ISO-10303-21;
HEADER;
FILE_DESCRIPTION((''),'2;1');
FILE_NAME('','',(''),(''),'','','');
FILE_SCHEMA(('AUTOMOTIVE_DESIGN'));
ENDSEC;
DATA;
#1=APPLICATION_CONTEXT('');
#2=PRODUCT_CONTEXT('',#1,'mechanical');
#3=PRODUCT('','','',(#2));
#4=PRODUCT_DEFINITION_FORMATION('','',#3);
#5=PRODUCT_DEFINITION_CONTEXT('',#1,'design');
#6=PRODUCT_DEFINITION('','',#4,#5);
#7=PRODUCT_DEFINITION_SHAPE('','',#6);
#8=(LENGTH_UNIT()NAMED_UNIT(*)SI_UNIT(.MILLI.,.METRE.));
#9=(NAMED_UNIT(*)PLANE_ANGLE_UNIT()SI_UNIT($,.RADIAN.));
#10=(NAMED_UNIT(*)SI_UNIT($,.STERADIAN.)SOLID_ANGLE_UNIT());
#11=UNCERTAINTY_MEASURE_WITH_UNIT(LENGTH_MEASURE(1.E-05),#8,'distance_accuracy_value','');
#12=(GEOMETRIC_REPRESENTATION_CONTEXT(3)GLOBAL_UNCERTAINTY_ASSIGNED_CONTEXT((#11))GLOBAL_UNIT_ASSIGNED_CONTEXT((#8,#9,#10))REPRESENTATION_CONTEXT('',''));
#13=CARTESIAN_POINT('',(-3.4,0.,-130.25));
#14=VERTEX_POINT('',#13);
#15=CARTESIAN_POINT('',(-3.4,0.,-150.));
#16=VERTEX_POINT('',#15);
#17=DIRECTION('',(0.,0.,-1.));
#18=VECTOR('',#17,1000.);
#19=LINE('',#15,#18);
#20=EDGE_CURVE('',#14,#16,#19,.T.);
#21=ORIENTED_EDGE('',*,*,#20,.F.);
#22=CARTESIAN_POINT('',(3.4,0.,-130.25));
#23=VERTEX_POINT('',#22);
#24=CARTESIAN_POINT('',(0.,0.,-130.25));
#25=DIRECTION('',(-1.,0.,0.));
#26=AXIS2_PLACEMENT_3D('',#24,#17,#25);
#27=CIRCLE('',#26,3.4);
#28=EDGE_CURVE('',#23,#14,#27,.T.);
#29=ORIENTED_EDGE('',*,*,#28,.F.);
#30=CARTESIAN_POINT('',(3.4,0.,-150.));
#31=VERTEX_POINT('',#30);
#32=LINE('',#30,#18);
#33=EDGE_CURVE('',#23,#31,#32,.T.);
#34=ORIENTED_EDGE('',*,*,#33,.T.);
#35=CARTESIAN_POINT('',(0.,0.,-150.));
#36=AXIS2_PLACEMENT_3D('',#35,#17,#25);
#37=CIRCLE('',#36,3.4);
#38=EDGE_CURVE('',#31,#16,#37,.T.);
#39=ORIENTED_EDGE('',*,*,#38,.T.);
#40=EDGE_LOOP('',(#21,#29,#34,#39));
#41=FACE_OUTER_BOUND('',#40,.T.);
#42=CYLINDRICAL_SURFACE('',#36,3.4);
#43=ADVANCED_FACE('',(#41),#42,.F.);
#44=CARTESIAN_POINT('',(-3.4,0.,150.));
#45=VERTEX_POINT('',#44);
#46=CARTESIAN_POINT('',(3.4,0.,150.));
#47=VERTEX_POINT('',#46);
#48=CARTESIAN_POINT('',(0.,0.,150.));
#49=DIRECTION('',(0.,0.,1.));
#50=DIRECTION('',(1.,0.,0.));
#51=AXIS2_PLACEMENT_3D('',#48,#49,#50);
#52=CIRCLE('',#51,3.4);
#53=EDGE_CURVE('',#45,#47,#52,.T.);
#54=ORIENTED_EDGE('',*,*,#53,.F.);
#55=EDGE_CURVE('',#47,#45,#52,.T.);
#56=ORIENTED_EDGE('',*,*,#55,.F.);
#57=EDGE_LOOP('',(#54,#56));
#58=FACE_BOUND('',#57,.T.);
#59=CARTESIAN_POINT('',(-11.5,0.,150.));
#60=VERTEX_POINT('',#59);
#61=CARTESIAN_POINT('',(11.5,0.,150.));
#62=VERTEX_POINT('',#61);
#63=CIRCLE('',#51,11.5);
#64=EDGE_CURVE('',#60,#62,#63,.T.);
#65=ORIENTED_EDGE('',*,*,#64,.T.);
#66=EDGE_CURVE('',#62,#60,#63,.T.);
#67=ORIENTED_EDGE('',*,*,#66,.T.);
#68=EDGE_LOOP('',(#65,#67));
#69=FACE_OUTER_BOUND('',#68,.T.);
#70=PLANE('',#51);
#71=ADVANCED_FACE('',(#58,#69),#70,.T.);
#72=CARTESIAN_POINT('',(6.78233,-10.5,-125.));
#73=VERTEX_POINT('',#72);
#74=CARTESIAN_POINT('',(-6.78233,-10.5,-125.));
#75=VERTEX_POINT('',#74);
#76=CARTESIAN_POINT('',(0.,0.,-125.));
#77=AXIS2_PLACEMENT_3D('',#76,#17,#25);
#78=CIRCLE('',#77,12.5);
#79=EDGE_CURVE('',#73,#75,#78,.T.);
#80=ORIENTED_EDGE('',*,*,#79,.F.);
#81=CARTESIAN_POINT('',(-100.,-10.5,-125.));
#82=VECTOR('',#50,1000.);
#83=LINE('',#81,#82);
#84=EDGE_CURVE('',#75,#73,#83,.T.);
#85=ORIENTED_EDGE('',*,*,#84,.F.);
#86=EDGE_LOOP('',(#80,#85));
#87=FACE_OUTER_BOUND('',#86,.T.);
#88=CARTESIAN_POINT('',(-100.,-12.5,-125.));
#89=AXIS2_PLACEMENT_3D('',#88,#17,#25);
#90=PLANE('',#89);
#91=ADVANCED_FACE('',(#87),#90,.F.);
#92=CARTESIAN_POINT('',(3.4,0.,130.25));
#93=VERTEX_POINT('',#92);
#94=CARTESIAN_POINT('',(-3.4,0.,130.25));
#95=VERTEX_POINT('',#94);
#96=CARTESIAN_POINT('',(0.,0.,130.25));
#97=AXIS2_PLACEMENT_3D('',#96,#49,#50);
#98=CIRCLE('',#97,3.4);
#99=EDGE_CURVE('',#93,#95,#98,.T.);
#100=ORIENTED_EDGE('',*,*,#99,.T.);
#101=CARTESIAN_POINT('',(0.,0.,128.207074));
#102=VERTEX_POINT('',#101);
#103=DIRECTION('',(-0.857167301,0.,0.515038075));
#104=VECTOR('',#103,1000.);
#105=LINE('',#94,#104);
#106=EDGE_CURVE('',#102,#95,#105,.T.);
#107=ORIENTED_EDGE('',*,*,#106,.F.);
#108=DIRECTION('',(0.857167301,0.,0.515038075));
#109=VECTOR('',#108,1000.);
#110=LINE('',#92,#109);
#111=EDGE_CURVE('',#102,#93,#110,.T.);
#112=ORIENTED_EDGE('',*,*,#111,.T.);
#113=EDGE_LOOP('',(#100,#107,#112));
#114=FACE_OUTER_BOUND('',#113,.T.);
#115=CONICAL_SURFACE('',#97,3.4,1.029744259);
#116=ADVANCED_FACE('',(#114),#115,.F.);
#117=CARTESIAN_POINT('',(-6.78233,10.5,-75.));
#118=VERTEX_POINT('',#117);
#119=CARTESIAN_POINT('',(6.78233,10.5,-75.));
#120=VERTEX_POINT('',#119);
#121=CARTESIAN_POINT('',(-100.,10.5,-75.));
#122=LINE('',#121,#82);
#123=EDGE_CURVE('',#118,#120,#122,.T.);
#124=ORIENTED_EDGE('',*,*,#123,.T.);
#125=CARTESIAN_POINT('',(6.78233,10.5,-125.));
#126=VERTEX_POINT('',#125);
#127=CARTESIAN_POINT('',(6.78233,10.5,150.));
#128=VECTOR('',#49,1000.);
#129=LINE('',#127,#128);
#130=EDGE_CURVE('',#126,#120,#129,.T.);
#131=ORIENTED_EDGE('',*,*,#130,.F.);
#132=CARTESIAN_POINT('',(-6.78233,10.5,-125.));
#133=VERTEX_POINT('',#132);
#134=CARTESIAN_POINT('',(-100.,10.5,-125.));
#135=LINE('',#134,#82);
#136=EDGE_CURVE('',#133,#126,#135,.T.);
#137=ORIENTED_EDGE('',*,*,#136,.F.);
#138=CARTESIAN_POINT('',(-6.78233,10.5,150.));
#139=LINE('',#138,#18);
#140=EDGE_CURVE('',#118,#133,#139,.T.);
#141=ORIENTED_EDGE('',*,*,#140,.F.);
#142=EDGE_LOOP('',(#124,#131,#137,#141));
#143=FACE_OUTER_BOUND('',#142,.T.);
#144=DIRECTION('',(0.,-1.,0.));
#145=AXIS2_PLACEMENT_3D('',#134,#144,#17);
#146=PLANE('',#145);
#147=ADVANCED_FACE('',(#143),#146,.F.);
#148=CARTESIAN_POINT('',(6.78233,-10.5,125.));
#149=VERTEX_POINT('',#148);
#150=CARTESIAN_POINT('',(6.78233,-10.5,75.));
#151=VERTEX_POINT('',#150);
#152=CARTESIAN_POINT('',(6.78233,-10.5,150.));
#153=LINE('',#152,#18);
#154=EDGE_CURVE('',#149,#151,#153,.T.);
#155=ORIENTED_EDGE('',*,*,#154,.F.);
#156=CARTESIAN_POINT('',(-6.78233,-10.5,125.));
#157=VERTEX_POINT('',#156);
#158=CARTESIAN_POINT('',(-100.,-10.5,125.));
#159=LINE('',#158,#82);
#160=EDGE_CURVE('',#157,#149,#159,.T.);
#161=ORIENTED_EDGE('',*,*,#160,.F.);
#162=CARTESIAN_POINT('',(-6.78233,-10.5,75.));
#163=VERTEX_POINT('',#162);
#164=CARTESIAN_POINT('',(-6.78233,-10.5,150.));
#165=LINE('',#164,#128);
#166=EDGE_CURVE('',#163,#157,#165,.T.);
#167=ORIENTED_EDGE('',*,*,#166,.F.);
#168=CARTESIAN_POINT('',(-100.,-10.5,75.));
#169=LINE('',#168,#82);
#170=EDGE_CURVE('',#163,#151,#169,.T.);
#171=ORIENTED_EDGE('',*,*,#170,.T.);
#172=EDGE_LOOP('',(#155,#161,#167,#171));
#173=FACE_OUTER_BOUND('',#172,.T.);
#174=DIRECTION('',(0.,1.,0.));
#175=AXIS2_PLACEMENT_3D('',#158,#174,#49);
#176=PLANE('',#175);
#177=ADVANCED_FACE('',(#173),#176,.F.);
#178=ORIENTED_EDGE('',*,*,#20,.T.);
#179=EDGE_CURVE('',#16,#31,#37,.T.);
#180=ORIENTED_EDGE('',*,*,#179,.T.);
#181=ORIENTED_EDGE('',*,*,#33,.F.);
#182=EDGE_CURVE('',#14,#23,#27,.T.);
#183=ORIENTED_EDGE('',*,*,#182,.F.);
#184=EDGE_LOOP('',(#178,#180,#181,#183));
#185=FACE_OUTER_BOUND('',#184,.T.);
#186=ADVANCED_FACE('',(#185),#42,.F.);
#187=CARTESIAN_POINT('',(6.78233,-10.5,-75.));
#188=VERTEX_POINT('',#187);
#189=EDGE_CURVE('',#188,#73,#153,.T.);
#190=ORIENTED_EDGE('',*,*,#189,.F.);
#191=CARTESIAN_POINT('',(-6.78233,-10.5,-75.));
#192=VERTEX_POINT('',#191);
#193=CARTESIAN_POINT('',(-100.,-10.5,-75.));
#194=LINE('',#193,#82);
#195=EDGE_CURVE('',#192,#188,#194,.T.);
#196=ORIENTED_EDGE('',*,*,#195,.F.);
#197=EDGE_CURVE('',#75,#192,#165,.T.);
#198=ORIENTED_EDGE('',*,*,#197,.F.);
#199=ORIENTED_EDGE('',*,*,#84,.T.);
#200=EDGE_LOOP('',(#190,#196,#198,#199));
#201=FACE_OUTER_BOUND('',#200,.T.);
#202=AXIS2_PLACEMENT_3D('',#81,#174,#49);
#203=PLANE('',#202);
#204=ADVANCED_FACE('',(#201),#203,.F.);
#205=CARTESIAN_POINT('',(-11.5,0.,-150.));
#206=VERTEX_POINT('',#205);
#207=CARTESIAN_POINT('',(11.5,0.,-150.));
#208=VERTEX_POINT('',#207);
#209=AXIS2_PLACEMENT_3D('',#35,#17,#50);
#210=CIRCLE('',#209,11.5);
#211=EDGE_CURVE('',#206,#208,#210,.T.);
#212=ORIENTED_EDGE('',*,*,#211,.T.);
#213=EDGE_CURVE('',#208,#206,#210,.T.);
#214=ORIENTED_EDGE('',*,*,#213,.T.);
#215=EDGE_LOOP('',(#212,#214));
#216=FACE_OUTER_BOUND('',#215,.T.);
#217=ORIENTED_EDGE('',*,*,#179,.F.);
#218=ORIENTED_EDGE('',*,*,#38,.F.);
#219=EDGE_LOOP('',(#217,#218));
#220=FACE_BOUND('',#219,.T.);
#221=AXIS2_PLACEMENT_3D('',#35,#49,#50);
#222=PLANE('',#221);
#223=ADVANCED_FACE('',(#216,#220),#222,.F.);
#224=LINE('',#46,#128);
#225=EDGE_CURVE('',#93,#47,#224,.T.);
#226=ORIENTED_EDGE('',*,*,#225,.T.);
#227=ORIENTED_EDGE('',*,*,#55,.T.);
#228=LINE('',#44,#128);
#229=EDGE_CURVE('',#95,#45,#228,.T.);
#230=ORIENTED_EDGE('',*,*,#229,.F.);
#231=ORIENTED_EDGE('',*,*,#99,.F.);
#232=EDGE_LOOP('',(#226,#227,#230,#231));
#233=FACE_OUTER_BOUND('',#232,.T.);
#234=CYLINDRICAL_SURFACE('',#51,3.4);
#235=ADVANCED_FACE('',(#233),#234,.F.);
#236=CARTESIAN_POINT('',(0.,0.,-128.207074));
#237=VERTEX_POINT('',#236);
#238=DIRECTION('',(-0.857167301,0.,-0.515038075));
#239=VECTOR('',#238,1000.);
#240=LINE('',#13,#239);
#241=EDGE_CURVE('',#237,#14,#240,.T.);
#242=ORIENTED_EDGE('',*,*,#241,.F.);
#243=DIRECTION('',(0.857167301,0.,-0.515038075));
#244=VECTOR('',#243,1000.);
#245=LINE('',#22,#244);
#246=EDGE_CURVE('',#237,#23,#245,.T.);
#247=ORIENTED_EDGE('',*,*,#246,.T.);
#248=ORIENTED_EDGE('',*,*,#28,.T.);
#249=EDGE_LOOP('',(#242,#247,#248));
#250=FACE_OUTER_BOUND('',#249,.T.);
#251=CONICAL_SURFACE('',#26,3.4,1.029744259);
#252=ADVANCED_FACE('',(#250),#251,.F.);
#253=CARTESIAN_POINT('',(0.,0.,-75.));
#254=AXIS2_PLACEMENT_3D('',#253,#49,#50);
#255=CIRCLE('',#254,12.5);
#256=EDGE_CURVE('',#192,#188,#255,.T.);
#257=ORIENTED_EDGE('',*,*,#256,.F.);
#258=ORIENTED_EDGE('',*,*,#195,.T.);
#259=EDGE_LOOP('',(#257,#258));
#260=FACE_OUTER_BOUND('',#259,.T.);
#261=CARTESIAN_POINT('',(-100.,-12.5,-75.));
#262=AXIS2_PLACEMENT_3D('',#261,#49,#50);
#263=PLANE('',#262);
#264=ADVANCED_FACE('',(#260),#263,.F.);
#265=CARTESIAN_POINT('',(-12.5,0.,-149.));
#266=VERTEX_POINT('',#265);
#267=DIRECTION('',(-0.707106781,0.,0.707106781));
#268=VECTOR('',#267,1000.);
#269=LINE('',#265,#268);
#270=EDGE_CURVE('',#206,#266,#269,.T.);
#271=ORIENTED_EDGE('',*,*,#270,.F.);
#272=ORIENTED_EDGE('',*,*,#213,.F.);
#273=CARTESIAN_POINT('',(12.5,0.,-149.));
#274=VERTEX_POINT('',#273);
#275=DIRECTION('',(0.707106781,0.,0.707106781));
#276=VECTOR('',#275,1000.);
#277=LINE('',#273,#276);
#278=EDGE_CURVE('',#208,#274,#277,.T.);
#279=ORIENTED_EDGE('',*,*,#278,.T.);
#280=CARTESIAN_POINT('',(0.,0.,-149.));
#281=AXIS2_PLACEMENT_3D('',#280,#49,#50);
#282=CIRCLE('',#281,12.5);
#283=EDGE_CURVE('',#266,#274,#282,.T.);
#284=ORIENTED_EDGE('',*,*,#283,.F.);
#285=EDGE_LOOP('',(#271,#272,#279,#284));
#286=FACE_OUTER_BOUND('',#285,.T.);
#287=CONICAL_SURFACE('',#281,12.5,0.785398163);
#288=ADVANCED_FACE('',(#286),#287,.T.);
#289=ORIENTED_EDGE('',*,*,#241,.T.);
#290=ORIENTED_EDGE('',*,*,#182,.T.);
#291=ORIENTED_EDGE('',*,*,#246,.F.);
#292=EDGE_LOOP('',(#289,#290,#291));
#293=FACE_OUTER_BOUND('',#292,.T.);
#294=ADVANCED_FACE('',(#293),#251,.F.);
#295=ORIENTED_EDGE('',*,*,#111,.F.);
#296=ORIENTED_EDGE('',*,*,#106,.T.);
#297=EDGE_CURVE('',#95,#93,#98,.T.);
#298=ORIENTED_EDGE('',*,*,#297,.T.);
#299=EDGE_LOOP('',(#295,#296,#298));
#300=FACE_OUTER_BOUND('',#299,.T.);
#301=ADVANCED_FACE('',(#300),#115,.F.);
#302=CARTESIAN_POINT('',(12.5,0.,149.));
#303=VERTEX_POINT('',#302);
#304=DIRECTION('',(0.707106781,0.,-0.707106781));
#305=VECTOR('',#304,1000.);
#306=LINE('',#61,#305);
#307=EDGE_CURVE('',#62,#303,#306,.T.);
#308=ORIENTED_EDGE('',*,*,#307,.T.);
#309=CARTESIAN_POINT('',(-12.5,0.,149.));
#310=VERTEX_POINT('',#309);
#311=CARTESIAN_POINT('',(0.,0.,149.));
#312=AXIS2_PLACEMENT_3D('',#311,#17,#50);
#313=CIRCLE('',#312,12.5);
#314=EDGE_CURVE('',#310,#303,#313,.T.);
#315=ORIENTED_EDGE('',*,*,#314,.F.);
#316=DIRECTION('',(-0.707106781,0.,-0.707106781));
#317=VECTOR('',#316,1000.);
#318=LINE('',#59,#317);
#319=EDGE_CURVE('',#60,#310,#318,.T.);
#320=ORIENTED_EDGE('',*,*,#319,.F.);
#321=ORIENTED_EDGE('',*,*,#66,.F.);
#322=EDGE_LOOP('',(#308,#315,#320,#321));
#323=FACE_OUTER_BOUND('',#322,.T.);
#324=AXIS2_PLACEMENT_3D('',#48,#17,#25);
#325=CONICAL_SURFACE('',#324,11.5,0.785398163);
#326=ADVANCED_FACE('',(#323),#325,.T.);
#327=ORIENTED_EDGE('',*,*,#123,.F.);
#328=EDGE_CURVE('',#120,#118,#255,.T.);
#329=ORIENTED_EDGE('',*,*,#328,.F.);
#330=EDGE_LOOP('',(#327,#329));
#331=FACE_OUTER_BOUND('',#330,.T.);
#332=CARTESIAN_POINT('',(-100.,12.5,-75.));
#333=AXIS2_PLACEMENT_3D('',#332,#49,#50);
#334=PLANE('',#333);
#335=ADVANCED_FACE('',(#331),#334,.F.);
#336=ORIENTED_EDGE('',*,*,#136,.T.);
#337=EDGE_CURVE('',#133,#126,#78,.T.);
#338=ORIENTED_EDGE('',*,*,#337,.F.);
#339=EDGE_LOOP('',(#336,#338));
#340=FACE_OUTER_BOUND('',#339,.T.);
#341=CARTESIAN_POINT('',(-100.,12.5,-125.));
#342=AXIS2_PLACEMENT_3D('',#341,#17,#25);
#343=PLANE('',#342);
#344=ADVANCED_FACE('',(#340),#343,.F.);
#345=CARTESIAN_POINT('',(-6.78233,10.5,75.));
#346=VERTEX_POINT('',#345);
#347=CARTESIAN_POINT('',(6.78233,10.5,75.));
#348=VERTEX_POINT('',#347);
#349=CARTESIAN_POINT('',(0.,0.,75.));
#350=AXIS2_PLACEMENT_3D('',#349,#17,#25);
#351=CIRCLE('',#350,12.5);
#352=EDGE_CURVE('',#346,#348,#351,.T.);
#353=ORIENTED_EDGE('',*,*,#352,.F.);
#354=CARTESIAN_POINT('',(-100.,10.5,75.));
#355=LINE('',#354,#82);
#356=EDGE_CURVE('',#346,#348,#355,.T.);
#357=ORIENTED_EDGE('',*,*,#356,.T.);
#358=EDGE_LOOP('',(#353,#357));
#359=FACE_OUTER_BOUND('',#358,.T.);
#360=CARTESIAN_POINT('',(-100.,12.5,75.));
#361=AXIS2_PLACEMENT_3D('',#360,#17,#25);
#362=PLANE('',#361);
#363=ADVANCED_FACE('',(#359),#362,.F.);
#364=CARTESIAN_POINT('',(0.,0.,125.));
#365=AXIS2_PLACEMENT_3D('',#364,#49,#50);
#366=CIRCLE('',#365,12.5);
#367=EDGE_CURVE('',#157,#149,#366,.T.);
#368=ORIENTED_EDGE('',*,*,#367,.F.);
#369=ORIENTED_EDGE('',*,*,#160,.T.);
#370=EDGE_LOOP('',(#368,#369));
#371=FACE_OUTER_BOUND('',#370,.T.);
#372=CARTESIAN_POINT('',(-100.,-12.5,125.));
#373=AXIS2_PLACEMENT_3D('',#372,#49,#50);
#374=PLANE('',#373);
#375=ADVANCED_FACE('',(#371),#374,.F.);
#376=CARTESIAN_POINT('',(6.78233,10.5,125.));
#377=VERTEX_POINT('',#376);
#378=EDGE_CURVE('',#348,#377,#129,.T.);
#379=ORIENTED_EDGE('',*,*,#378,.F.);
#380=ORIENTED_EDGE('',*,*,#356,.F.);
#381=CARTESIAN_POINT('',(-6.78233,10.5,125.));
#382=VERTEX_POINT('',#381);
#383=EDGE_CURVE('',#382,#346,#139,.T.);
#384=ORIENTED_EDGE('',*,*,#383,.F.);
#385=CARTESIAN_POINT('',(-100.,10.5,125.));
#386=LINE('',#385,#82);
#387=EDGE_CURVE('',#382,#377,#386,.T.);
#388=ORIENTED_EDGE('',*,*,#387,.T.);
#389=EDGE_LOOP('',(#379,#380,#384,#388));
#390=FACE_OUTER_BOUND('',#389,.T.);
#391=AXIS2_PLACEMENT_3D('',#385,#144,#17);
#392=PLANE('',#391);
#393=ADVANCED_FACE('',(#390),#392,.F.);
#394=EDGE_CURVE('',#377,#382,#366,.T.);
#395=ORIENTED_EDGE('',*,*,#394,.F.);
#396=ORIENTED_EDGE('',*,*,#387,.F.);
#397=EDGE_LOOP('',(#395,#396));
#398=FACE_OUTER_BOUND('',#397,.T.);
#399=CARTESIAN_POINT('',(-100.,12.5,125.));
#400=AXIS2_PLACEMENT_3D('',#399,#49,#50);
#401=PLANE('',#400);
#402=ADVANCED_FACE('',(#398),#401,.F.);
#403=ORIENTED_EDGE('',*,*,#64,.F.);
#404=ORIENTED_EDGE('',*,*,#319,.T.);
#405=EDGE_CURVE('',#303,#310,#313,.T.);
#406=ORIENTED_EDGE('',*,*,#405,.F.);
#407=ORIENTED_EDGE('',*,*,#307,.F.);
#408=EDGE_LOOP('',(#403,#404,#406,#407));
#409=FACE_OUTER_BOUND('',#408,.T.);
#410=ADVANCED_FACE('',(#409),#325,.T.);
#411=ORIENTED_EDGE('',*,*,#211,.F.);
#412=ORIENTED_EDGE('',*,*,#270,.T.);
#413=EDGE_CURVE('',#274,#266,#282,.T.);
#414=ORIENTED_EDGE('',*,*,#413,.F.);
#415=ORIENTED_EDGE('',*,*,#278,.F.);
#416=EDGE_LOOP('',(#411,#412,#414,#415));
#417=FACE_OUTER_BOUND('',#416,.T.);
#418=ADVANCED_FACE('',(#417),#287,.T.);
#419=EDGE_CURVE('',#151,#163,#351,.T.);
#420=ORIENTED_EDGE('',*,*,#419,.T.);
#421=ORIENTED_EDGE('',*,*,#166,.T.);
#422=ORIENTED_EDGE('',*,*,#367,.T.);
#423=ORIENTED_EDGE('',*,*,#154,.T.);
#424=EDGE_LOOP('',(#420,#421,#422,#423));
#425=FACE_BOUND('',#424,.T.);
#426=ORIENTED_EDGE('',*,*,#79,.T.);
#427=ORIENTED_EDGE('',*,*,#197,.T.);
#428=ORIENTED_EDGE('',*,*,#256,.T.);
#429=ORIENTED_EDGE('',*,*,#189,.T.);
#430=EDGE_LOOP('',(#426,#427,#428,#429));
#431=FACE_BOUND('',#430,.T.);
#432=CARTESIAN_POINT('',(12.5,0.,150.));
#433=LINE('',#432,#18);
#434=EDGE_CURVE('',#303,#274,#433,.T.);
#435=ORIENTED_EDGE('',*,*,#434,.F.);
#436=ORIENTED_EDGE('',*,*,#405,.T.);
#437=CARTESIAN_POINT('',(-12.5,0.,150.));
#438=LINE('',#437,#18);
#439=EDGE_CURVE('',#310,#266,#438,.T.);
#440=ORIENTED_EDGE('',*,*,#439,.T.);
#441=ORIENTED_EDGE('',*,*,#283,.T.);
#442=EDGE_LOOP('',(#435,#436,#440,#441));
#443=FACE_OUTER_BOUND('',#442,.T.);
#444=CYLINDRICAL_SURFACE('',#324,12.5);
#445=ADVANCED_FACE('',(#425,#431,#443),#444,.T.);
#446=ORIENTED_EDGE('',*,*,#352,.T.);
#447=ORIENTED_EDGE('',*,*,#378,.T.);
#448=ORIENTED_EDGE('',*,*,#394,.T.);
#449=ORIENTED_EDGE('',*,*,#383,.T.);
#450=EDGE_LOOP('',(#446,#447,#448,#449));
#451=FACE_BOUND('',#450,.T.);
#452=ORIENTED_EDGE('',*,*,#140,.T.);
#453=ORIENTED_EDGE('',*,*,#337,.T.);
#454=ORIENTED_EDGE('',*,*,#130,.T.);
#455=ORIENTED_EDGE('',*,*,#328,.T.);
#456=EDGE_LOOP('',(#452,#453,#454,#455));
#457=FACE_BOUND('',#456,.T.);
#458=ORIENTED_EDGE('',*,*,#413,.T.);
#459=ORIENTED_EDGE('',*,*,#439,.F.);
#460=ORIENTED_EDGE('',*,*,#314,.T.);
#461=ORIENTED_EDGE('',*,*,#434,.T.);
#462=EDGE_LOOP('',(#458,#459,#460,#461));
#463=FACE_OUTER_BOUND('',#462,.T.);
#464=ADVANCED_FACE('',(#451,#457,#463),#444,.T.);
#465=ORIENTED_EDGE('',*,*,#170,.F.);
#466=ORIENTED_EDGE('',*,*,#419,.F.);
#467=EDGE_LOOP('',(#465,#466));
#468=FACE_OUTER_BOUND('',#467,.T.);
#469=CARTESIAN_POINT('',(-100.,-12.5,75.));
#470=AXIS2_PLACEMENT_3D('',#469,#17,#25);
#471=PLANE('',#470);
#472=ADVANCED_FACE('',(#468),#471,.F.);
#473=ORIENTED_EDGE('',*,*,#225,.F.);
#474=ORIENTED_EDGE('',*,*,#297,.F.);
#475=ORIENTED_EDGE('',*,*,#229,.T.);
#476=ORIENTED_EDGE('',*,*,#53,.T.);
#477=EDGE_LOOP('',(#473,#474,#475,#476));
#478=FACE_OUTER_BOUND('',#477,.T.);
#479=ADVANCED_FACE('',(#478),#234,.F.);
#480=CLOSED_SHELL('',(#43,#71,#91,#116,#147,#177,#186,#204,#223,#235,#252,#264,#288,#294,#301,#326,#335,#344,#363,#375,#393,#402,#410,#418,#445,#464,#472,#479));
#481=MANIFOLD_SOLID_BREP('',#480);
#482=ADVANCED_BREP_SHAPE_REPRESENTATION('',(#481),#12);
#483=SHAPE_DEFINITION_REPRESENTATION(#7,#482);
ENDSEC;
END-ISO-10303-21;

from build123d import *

# Parameters (mm, degrees)
SKETCH_1_R          = 12.5
EXTRUDE_1_DEPTH     = 150
SKETCH_2_W          = 50
SKETCH_2_H          = 2
CUT_EXTRUDE_1_DEPTH = 100
CHAMFER_1_SIZE      = 1


with BuildPart() as part:
    # 草图1 → 凸台-拉伸1 (new, symmetric)
    with BuildSketch(Plane.XY):
        Circle(SKETCH_1_R)
    extrude(amount=EXTRUDE_1_DEPTH, both=True)

    # 草图2 → 切除-拉伸1 (cut, symmetric)
    with BuildSketch(Plane(origin=(0, 0, 0), x_dir=(0, 0, -1), z_dir=(1, 0, 0))):
        with Locations((-100, 11.5)):
            Rectangle(SKETCH_2_W, SKETCH_2_H)
        with Locations((-100, -11.5)):
            Rectangle(SKETCH_2_W, SKETCH_2_H)
        with Locations((100, -11.5)):
            Rectangle(SKETCH_2_W, SKETCH_2_H)
        with Locations((100, 11.5)):
            Rectangle(SKETCH_2_W, SKETCH_2_H)
    extrude(amount=CUT_EXTRUDE_1_DEPTH, both=True, mode=Mode.SUBTRACT)

    # 倒角1
    chamfer_1_edges = [part.edges().sort_by_distance(p)[0] for p in [
        (-12.5, 0, -150),
        (-12.5, 0, 150),
    ]]
    chamfer(chamfer_1_edges, length=CHAMFER_1_SIZE)

    # 草图4 → M8 螺纹孔1 (revolve, cut)
    with BuildSketch(Plane(origin=(0, 0, -150), x_dir=(0, 1, 0), z_dir=(1, 0, 0))):
        Polygon((0, 0), (0, 21.792926105), (3.4, 19.75), (3.4, 0), align=None)
    hole_wizard_m8_1 = revolve(axis=Axis((0, 0, -156.35), (0, 0, 1)), mode=Mode.SUBTRACT)

    # 镜向1: M8 螺纹孔1 across plane
    add(hole_wizard_m8_1.mirror(Plane.XY), mode=Mode.SUBTRACT)


solid = part.part
